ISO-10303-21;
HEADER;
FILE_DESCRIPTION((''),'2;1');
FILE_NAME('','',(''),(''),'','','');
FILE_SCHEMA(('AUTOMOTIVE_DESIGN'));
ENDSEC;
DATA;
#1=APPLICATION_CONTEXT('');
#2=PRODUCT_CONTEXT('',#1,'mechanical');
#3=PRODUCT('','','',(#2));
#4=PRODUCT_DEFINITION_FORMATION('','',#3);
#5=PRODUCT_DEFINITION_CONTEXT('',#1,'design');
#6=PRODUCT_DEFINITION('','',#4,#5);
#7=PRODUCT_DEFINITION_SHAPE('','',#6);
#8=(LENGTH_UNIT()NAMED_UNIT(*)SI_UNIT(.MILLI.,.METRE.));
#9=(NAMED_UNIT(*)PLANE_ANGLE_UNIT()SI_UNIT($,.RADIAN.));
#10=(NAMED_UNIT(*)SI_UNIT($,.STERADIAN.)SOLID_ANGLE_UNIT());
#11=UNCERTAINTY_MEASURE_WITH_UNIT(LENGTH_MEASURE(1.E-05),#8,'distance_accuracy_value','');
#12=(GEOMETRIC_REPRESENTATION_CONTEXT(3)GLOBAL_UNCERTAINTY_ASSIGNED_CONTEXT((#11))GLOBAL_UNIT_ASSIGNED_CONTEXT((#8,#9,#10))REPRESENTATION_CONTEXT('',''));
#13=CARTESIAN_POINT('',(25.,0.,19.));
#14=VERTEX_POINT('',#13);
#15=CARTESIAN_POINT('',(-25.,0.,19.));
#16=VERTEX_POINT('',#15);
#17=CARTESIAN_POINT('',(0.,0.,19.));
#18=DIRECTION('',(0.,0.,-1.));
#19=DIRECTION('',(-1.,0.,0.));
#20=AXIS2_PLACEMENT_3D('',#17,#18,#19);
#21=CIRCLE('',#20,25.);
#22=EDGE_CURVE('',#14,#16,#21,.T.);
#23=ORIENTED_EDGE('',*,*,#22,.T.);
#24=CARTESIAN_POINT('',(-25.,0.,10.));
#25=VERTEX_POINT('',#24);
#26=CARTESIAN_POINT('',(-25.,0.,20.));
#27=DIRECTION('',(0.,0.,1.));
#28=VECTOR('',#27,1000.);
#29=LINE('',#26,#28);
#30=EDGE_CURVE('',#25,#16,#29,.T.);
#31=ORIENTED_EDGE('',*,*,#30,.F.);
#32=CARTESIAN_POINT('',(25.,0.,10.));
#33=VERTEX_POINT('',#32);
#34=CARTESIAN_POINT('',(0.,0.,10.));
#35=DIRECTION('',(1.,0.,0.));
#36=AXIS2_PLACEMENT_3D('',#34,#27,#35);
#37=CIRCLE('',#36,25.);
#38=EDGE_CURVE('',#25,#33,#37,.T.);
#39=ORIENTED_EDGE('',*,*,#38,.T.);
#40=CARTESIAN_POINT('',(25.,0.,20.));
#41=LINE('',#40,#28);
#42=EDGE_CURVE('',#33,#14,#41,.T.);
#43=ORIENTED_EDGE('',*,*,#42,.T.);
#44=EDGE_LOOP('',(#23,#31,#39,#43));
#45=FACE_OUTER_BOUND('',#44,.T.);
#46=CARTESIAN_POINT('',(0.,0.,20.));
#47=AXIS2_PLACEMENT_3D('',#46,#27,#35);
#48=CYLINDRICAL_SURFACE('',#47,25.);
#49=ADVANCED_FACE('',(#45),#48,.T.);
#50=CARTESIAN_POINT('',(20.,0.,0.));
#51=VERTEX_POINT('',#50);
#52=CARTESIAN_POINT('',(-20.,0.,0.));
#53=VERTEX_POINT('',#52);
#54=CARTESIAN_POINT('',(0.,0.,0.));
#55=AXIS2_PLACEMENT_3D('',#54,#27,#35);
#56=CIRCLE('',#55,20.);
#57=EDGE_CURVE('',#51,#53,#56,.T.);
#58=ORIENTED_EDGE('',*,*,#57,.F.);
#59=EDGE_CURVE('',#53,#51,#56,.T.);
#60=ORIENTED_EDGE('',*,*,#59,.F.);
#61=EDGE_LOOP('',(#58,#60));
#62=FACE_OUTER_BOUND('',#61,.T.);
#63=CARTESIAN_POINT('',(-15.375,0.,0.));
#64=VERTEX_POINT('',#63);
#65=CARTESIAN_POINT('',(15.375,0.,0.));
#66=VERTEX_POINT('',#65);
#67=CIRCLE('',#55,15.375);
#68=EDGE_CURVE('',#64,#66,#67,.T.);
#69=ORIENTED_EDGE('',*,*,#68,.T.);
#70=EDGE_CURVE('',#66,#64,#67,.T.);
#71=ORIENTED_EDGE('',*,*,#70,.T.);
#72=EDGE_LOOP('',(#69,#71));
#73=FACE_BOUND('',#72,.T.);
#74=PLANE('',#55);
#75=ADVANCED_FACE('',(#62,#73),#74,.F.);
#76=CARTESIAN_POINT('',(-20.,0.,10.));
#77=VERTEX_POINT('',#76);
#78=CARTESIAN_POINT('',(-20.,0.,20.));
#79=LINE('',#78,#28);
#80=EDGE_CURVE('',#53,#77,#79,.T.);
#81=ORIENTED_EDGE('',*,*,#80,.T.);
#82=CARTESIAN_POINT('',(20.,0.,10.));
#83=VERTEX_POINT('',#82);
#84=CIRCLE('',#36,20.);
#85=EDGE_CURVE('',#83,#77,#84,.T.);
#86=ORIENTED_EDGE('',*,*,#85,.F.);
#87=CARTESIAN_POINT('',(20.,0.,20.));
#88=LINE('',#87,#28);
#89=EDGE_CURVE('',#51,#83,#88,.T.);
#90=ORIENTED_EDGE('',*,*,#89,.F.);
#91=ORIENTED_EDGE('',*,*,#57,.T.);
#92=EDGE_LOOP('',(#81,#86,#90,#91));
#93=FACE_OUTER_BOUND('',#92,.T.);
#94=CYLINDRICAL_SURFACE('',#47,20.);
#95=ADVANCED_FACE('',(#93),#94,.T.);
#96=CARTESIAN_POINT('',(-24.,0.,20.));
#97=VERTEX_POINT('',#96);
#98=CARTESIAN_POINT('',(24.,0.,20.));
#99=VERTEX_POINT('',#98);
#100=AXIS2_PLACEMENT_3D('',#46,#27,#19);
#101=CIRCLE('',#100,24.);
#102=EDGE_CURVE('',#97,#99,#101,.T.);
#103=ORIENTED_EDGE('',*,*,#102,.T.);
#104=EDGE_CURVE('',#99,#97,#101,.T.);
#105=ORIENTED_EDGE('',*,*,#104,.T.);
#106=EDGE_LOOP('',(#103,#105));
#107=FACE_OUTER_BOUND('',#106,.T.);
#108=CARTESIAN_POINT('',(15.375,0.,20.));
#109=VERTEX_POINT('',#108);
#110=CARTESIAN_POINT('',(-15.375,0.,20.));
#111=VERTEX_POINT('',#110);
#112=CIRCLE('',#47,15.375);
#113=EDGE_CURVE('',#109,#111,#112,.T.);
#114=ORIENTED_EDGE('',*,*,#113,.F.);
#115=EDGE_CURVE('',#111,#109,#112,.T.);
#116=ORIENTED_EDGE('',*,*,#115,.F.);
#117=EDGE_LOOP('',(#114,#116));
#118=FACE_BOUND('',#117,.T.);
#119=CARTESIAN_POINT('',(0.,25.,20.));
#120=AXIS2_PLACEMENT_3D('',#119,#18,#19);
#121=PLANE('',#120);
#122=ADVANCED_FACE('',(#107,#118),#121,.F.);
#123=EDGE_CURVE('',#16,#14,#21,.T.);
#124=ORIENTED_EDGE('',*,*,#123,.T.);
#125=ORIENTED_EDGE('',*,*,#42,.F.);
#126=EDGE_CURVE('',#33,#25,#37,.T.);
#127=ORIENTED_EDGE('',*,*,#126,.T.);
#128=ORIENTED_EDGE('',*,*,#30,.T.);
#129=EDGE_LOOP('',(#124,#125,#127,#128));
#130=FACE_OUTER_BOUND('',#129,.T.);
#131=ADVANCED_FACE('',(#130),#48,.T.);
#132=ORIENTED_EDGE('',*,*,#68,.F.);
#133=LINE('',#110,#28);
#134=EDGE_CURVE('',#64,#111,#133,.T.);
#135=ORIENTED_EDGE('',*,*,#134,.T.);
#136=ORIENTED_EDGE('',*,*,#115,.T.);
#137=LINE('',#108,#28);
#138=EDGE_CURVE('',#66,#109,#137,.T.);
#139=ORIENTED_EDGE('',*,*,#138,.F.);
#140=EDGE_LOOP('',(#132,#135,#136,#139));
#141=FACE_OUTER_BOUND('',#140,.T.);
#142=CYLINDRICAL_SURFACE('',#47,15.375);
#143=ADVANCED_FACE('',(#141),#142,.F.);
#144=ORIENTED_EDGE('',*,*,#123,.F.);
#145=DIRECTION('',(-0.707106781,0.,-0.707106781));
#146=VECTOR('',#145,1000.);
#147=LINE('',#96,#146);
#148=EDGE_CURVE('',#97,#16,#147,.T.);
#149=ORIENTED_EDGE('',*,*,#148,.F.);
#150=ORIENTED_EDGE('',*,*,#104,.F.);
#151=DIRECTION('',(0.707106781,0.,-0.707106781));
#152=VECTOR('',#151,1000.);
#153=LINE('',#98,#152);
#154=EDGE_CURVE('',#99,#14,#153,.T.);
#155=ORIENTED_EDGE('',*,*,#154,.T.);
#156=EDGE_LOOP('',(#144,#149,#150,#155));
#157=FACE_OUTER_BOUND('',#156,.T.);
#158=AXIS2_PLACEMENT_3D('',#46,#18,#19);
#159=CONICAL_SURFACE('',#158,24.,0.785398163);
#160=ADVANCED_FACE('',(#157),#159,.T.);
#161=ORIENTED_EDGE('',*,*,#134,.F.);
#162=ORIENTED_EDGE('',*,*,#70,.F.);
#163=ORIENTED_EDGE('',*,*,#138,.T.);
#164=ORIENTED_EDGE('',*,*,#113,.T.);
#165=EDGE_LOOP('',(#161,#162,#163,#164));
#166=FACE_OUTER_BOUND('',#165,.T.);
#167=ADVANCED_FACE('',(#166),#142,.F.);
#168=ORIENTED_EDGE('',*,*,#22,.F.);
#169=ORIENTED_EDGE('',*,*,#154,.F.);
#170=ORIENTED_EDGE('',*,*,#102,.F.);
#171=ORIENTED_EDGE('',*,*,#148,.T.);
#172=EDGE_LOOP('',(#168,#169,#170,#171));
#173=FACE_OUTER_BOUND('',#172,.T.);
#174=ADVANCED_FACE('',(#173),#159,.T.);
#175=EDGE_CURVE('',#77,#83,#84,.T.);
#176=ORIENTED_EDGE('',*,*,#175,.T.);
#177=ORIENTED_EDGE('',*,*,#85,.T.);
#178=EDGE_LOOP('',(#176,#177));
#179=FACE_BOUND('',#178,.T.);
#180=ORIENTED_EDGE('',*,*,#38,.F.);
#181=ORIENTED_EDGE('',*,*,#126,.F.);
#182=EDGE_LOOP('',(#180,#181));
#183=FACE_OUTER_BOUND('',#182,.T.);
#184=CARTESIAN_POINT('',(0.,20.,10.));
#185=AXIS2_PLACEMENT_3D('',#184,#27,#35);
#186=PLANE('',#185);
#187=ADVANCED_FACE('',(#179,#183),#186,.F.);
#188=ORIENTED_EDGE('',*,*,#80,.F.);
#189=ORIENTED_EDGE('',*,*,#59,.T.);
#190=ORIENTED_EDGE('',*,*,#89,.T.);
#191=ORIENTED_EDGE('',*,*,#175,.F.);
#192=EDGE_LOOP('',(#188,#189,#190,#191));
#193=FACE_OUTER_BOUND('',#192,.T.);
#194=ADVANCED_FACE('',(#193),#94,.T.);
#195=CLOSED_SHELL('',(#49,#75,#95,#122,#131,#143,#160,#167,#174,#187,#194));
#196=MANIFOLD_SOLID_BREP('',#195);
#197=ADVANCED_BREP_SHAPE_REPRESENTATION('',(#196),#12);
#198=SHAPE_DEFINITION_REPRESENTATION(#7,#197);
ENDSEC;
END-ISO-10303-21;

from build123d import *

# Parameters (mm, degrees)
G1_TAPPED_HOLE1_D = 30.75
CHAMFER1_SIZE     = 1


with BuildPart() as part:
    # Sketch1 → Revolve1 (revolve)
    with BuildSketch(Plane(origin=(0, 0, 0), x_dir=(0, 0, -1), z_dir=(1, 0, 0)), mode=Mode.PRIVATE) as revolve1_sk:
        Polygon((0, 0), (0, 20), (-10, 20), (-10, 25), (-20, 25), (-20, 0), align=None)
    revolve(revolve1_sk.sketch.rotate(Axis((0, 0, 20), (0, 0, -1)), 90), axis=Axis((0, 0, 20), (0, 0, -1)))

    # G1 Tapped Hole1 (through all)
    with Locations(Plane.XY.offset(20)):
        with Locations((0, 0)):
            Hole(G1_TAPPED_HOLE1_D / 2)

    # Chamfer1
    chamfer1_edges = [part.edges().sort_by_distance(p)[0] for p in [
        (-25, 0, 20),
    ]]
    chamfer(chamfer1_edges, length=CHAMFER1_SIZE)


solid = part.part
